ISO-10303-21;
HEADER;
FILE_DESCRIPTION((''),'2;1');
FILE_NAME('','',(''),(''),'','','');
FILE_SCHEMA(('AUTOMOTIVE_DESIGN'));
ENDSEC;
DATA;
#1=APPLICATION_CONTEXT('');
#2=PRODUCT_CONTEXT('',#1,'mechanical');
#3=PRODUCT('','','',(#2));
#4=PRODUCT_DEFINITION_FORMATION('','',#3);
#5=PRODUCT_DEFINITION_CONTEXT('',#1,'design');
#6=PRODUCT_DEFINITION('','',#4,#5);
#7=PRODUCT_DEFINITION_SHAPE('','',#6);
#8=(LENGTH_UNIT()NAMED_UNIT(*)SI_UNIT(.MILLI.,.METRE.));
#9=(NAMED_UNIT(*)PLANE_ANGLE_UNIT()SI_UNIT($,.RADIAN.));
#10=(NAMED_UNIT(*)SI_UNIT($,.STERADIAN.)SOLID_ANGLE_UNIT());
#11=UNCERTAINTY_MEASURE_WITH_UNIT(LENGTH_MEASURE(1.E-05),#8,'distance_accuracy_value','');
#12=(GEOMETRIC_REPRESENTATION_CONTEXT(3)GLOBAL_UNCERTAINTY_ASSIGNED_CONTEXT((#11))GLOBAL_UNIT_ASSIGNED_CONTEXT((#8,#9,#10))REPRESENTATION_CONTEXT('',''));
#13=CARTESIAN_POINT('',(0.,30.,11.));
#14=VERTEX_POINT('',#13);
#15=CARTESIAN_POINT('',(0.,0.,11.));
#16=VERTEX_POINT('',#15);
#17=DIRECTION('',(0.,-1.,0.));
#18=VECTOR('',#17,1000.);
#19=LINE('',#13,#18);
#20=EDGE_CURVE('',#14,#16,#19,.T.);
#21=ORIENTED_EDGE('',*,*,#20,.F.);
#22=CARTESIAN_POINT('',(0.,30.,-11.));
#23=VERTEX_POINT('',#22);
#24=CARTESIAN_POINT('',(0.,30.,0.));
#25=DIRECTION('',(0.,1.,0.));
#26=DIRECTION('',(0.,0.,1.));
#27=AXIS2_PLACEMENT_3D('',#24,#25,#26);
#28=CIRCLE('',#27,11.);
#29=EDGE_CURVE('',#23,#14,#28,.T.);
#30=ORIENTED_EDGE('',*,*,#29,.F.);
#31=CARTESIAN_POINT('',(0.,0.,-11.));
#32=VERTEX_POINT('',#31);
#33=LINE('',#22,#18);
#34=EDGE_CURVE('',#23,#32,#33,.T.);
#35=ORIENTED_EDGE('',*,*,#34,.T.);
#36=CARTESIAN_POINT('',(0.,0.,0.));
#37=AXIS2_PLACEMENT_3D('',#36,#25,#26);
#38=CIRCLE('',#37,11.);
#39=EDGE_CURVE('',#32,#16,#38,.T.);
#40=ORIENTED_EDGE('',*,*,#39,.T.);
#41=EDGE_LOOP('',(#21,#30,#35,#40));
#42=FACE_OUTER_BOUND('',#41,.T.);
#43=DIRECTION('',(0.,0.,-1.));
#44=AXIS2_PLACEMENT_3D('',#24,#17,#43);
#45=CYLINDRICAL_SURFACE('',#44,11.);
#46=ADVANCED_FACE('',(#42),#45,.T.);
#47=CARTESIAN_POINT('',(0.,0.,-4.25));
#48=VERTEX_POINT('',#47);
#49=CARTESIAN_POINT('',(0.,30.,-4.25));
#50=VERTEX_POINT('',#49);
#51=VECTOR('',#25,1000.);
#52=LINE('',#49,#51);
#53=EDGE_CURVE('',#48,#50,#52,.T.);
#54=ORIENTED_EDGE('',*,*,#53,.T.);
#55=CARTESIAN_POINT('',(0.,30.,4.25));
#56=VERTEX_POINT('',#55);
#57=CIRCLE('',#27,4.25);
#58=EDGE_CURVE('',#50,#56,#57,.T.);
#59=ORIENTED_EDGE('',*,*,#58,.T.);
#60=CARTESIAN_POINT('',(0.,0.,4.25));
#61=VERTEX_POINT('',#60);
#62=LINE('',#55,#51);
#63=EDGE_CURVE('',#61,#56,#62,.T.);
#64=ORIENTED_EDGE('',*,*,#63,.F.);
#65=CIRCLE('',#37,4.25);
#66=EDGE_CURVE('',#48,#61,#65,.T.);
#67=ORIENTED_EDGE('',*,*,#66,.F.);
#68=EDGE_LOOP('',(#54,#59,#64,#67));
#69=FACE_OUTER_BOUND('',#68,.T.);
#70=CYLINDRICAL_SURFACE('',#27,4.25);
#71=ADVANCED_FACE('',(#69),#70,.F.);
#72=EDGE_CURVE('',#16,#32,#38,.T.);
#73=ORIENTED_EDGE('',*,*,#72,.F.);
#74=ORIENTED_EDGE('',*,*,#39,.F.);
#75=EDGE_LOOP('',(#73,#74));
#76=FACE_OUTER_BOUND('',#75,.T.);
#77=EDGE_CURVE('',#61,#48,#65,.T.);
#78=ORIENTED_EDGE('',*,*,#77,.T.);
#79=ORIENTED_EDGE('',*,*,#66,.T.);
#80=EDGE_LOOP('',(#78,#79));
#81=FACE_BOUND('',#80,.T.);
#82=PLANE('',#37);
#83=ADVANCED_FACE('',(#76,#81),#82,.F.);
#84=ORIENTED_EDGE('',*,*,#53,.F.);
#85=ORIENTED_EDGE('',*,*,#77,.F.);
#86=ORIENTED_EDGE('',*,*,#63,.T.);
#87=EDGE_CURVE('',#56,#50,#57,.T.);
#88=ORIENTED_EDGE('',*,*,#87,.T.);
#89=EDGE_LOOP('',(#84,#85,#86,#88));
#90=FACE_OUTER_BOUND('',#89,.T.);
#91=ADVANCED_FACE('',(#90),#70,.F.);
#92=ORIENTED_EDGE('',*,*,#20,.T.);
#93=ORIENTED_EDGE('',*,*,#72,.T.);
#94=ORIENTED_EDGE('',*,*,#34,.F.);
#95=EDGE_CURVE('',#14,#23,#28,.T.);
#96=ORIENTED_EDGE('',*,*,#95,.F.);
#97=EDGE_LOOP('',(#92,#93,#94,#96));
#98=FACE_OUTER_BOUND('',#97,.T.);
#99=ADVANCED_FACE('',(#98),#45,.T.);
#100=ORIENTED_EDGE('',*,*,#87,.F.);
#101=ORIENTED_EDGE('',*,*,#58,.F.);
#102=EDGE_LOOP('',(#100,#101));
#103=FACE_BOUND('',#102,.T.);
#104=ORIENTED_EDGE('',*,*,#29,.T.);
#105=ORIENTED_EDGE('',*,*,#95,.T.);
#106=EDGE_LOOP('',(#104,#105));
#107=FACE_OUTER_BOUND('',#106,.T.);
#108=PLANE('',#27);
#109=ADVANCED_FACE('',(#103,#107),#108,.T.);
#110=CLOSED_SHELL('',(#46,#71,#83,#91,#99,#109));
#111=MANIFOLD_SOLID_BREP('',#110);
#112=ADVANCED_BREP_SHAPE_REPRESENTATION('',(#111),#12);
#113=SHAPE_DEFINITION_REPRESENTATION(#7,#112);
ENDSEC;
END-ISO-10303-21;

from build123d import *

# Parameters (mm, degrees)
SKETCH1_R              = 11
BOSS_EXTRUDE1_DEPTH    = 30
M10_TAPPED_HOLE1_D     = 8.5
M10_TAPPED_HOLE1_DEPTH = 35
M10_TAPPED_HOLE1_TIP   = 2.553657631


with BuildPart() as part:
    # Sketch1 → Boss-Extrude1 (new body)
    with BuildSketch(Plane(origin=(0, 0, 0), x_dir=(1, 0, 0), z_dir=(0, 1, 0))):
        with Locations(Location((0, 0, 0), (0, 0, 270))):
            Circle(SKETCH1_R)
    extrude(amount=BOSS_EXTRUDE1_DEPTH)

    # M10 Tapped Hole1
    with Locations(Plane(origin=(0, 30, 0), x_dir=(1, 0, 0), z_dir=(0, 1, 0))):
        with Locations((0, 0)):
            Hole(M10_TAPPED_HOLE1_D / 2, depth=M10_TAPPED_HOLE1_DEPTH)
            with Locations((0, 0, -(M10_TAPPED_HOLE1_DEPTH + M10_TAPPED_HOLE1_TIP / 2))):  # 118° drill point
                Cone(0, M10_TAPPED_HOLE1_D / 2, M10_TAPPED_HOLE1_TIP, mode=Mode.SUBTRACT)


solid = part.part
